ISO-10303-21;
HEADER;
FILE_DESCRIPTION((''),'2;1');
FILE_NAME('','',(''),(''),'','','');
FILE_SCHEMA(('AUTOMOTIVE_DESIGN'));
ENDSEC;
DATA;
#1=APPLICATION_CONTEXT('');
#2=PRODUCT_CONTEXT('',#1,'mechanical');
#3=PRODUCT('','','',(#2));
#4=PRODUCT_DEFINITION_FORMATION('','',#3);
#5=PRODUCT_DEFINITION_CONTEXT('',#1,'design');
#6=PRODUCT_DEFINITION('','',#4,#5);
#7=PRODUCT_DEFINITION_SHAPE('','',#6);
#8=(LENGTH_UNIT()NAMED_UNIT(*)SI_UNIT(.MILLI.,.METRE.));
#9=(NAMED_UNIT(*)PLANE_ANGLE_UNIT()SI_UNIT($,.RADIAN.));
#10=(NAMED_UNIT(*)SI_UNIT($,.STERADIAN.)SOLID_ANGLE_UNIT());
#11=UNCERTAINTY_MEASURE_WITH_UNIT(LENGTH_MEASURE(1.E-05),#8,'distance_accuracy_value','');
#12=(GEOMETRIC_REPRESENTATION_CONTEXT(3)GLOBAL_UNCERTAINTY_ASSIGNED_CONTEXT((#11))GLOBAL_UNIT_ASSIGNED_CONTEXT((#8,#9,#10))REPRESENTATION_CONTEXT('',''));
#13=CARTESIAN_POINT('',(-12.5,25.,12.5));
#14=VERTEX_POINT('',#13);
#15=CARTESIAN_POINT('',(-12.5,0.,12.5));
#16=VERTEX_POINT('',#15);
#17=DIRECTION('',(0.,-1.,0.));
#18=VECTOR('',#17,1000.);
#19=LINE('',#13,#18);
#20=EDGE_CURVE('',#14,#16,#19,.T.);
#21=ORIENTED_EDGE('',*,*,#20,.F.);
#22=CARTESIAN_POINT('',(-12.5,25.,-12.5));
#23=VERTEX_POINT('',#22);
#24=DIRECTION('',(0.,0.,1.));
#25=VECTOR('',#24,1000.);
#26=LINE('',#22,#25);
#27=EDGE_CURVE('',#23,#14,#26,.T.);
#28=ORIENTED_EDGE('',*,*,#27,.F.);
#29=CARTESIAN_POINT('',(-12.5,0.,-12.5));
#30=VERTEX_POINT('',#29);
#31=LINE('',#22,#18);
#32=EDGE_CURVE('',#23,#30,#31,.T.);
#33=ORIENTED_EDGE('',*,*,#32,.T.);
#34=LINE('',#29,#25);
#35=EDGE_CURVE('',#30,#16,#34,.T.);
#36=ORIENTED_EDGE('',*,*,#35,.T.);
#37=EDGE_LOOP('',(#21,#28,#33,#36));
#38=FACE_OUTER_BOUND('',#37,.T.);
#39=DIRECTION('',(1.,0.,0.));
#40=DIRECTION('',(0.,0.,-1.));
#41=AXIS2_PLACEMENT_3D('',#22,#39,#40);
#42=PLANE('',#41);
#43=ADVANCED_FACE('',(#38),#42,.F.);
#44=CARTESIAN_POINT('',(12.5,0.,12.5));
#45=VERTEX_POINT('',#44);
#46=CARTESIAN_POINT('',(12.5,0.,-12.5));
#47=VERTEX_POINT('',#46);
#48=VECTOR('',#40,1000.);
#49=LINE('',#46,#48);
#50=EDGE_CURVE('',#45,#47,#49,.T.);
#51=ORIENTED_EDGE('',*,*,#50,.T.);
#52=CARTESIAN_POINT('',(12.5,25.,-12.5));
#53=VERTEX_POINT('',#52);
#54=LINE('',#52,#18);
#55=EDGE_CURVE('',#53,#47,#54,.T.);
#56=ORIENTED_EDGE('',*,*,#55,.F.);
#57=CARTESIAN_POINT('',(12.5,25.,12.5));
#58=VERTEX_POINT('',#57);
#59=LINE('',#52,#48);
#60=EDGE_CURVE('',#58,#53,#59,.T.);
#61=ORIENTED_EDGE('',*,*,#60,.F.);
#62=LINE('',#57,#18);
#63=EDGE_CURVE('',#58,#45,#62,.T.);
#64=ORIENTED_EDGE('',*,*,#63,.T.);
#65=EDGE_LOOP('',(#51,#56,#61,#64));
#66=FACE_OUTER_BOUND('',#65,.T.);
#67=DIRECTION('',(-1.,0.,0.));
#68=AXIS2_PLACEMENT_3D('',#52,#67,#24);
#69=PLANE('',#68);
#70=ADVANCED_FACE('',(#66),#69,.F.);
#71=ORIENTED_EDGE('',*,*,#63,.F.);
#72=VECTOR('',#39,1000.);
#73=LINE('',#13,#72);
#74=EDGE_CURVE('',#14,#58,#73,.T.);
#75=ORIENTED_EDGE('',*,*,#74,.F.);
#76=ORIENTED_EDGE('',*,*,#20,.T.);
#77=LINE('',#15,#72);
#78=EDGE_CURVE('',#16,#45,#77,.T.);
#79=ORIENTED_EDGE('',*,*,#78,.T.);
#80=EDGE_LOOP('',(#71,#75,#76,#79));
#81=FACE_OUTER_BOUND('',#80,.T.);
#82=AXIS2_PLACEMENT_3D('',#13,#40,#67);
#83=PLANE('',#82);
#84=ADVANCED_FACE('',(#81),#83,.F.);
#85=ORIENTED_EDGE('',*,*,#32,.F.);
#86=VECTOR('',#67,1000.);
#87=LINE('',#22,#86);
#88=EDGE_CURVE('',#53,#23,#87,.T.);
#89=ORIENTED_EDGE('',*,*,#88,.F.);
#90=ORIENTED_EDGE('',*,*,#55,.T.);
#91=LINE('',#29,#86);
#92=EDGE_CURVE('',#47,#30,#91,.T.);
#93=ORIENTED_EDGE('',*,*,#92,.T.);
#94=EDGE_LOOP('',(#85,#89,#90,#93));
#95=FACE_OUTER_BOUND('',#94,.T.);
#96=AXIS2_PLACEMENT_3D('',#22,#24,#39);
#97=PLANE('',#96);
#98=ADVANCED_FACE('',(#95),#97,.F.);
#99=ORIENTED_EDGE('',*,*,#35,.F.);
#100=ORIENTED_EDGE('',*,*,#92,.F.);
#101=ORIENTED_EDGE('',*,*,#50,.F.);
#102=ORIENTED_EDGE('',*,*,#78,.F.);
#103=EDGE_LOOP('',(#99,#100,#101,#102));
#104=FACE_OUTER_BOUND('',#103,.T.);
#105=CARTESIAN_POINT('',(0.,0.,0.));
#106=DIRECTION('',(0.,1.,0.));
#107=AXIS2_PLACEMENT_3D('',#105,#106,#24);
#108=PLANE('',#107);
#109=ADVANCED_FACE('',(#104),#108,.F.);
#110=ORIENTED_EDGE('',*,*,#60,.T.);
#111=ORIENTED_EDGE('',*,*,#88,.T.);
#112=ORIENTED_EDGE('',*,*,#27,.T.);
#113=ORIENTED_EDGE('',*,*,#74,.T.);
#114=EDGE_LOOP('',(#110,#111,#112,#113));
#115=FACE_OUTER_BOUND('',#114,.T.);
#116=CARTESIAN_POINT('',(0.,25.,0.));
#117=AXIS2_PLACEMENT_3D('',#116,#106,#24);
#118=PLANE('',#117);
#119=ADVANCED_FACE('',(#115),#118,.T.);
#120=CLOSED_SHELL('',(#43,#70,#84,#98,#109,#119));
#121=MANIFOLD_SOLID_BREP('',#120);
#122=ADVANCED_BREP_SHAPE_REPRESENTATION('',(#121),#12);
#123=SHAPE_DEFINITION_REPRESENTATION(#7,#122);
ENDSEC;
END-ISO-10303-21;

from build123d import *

# Parameters (mm, degrees)
SKETCH1_W           = 25
SKETCH1_H           = 25
BOSS_EXTRUDE1_DEPTH = 25


with BuildPart() as part:
    # Sketch1 → Boss-Extrude1 (new body)
    with BuildSketch(Plane(origin=(0, 0, 0), x_dir=(1, 0, 0), z_dir=(0, 1, 0))):
        Rectangle(SKETCH1_W, SKETCH1_H)
    extrude(amount=BOSS_EXTRUDE1_DEPTH)


solid = part.part
